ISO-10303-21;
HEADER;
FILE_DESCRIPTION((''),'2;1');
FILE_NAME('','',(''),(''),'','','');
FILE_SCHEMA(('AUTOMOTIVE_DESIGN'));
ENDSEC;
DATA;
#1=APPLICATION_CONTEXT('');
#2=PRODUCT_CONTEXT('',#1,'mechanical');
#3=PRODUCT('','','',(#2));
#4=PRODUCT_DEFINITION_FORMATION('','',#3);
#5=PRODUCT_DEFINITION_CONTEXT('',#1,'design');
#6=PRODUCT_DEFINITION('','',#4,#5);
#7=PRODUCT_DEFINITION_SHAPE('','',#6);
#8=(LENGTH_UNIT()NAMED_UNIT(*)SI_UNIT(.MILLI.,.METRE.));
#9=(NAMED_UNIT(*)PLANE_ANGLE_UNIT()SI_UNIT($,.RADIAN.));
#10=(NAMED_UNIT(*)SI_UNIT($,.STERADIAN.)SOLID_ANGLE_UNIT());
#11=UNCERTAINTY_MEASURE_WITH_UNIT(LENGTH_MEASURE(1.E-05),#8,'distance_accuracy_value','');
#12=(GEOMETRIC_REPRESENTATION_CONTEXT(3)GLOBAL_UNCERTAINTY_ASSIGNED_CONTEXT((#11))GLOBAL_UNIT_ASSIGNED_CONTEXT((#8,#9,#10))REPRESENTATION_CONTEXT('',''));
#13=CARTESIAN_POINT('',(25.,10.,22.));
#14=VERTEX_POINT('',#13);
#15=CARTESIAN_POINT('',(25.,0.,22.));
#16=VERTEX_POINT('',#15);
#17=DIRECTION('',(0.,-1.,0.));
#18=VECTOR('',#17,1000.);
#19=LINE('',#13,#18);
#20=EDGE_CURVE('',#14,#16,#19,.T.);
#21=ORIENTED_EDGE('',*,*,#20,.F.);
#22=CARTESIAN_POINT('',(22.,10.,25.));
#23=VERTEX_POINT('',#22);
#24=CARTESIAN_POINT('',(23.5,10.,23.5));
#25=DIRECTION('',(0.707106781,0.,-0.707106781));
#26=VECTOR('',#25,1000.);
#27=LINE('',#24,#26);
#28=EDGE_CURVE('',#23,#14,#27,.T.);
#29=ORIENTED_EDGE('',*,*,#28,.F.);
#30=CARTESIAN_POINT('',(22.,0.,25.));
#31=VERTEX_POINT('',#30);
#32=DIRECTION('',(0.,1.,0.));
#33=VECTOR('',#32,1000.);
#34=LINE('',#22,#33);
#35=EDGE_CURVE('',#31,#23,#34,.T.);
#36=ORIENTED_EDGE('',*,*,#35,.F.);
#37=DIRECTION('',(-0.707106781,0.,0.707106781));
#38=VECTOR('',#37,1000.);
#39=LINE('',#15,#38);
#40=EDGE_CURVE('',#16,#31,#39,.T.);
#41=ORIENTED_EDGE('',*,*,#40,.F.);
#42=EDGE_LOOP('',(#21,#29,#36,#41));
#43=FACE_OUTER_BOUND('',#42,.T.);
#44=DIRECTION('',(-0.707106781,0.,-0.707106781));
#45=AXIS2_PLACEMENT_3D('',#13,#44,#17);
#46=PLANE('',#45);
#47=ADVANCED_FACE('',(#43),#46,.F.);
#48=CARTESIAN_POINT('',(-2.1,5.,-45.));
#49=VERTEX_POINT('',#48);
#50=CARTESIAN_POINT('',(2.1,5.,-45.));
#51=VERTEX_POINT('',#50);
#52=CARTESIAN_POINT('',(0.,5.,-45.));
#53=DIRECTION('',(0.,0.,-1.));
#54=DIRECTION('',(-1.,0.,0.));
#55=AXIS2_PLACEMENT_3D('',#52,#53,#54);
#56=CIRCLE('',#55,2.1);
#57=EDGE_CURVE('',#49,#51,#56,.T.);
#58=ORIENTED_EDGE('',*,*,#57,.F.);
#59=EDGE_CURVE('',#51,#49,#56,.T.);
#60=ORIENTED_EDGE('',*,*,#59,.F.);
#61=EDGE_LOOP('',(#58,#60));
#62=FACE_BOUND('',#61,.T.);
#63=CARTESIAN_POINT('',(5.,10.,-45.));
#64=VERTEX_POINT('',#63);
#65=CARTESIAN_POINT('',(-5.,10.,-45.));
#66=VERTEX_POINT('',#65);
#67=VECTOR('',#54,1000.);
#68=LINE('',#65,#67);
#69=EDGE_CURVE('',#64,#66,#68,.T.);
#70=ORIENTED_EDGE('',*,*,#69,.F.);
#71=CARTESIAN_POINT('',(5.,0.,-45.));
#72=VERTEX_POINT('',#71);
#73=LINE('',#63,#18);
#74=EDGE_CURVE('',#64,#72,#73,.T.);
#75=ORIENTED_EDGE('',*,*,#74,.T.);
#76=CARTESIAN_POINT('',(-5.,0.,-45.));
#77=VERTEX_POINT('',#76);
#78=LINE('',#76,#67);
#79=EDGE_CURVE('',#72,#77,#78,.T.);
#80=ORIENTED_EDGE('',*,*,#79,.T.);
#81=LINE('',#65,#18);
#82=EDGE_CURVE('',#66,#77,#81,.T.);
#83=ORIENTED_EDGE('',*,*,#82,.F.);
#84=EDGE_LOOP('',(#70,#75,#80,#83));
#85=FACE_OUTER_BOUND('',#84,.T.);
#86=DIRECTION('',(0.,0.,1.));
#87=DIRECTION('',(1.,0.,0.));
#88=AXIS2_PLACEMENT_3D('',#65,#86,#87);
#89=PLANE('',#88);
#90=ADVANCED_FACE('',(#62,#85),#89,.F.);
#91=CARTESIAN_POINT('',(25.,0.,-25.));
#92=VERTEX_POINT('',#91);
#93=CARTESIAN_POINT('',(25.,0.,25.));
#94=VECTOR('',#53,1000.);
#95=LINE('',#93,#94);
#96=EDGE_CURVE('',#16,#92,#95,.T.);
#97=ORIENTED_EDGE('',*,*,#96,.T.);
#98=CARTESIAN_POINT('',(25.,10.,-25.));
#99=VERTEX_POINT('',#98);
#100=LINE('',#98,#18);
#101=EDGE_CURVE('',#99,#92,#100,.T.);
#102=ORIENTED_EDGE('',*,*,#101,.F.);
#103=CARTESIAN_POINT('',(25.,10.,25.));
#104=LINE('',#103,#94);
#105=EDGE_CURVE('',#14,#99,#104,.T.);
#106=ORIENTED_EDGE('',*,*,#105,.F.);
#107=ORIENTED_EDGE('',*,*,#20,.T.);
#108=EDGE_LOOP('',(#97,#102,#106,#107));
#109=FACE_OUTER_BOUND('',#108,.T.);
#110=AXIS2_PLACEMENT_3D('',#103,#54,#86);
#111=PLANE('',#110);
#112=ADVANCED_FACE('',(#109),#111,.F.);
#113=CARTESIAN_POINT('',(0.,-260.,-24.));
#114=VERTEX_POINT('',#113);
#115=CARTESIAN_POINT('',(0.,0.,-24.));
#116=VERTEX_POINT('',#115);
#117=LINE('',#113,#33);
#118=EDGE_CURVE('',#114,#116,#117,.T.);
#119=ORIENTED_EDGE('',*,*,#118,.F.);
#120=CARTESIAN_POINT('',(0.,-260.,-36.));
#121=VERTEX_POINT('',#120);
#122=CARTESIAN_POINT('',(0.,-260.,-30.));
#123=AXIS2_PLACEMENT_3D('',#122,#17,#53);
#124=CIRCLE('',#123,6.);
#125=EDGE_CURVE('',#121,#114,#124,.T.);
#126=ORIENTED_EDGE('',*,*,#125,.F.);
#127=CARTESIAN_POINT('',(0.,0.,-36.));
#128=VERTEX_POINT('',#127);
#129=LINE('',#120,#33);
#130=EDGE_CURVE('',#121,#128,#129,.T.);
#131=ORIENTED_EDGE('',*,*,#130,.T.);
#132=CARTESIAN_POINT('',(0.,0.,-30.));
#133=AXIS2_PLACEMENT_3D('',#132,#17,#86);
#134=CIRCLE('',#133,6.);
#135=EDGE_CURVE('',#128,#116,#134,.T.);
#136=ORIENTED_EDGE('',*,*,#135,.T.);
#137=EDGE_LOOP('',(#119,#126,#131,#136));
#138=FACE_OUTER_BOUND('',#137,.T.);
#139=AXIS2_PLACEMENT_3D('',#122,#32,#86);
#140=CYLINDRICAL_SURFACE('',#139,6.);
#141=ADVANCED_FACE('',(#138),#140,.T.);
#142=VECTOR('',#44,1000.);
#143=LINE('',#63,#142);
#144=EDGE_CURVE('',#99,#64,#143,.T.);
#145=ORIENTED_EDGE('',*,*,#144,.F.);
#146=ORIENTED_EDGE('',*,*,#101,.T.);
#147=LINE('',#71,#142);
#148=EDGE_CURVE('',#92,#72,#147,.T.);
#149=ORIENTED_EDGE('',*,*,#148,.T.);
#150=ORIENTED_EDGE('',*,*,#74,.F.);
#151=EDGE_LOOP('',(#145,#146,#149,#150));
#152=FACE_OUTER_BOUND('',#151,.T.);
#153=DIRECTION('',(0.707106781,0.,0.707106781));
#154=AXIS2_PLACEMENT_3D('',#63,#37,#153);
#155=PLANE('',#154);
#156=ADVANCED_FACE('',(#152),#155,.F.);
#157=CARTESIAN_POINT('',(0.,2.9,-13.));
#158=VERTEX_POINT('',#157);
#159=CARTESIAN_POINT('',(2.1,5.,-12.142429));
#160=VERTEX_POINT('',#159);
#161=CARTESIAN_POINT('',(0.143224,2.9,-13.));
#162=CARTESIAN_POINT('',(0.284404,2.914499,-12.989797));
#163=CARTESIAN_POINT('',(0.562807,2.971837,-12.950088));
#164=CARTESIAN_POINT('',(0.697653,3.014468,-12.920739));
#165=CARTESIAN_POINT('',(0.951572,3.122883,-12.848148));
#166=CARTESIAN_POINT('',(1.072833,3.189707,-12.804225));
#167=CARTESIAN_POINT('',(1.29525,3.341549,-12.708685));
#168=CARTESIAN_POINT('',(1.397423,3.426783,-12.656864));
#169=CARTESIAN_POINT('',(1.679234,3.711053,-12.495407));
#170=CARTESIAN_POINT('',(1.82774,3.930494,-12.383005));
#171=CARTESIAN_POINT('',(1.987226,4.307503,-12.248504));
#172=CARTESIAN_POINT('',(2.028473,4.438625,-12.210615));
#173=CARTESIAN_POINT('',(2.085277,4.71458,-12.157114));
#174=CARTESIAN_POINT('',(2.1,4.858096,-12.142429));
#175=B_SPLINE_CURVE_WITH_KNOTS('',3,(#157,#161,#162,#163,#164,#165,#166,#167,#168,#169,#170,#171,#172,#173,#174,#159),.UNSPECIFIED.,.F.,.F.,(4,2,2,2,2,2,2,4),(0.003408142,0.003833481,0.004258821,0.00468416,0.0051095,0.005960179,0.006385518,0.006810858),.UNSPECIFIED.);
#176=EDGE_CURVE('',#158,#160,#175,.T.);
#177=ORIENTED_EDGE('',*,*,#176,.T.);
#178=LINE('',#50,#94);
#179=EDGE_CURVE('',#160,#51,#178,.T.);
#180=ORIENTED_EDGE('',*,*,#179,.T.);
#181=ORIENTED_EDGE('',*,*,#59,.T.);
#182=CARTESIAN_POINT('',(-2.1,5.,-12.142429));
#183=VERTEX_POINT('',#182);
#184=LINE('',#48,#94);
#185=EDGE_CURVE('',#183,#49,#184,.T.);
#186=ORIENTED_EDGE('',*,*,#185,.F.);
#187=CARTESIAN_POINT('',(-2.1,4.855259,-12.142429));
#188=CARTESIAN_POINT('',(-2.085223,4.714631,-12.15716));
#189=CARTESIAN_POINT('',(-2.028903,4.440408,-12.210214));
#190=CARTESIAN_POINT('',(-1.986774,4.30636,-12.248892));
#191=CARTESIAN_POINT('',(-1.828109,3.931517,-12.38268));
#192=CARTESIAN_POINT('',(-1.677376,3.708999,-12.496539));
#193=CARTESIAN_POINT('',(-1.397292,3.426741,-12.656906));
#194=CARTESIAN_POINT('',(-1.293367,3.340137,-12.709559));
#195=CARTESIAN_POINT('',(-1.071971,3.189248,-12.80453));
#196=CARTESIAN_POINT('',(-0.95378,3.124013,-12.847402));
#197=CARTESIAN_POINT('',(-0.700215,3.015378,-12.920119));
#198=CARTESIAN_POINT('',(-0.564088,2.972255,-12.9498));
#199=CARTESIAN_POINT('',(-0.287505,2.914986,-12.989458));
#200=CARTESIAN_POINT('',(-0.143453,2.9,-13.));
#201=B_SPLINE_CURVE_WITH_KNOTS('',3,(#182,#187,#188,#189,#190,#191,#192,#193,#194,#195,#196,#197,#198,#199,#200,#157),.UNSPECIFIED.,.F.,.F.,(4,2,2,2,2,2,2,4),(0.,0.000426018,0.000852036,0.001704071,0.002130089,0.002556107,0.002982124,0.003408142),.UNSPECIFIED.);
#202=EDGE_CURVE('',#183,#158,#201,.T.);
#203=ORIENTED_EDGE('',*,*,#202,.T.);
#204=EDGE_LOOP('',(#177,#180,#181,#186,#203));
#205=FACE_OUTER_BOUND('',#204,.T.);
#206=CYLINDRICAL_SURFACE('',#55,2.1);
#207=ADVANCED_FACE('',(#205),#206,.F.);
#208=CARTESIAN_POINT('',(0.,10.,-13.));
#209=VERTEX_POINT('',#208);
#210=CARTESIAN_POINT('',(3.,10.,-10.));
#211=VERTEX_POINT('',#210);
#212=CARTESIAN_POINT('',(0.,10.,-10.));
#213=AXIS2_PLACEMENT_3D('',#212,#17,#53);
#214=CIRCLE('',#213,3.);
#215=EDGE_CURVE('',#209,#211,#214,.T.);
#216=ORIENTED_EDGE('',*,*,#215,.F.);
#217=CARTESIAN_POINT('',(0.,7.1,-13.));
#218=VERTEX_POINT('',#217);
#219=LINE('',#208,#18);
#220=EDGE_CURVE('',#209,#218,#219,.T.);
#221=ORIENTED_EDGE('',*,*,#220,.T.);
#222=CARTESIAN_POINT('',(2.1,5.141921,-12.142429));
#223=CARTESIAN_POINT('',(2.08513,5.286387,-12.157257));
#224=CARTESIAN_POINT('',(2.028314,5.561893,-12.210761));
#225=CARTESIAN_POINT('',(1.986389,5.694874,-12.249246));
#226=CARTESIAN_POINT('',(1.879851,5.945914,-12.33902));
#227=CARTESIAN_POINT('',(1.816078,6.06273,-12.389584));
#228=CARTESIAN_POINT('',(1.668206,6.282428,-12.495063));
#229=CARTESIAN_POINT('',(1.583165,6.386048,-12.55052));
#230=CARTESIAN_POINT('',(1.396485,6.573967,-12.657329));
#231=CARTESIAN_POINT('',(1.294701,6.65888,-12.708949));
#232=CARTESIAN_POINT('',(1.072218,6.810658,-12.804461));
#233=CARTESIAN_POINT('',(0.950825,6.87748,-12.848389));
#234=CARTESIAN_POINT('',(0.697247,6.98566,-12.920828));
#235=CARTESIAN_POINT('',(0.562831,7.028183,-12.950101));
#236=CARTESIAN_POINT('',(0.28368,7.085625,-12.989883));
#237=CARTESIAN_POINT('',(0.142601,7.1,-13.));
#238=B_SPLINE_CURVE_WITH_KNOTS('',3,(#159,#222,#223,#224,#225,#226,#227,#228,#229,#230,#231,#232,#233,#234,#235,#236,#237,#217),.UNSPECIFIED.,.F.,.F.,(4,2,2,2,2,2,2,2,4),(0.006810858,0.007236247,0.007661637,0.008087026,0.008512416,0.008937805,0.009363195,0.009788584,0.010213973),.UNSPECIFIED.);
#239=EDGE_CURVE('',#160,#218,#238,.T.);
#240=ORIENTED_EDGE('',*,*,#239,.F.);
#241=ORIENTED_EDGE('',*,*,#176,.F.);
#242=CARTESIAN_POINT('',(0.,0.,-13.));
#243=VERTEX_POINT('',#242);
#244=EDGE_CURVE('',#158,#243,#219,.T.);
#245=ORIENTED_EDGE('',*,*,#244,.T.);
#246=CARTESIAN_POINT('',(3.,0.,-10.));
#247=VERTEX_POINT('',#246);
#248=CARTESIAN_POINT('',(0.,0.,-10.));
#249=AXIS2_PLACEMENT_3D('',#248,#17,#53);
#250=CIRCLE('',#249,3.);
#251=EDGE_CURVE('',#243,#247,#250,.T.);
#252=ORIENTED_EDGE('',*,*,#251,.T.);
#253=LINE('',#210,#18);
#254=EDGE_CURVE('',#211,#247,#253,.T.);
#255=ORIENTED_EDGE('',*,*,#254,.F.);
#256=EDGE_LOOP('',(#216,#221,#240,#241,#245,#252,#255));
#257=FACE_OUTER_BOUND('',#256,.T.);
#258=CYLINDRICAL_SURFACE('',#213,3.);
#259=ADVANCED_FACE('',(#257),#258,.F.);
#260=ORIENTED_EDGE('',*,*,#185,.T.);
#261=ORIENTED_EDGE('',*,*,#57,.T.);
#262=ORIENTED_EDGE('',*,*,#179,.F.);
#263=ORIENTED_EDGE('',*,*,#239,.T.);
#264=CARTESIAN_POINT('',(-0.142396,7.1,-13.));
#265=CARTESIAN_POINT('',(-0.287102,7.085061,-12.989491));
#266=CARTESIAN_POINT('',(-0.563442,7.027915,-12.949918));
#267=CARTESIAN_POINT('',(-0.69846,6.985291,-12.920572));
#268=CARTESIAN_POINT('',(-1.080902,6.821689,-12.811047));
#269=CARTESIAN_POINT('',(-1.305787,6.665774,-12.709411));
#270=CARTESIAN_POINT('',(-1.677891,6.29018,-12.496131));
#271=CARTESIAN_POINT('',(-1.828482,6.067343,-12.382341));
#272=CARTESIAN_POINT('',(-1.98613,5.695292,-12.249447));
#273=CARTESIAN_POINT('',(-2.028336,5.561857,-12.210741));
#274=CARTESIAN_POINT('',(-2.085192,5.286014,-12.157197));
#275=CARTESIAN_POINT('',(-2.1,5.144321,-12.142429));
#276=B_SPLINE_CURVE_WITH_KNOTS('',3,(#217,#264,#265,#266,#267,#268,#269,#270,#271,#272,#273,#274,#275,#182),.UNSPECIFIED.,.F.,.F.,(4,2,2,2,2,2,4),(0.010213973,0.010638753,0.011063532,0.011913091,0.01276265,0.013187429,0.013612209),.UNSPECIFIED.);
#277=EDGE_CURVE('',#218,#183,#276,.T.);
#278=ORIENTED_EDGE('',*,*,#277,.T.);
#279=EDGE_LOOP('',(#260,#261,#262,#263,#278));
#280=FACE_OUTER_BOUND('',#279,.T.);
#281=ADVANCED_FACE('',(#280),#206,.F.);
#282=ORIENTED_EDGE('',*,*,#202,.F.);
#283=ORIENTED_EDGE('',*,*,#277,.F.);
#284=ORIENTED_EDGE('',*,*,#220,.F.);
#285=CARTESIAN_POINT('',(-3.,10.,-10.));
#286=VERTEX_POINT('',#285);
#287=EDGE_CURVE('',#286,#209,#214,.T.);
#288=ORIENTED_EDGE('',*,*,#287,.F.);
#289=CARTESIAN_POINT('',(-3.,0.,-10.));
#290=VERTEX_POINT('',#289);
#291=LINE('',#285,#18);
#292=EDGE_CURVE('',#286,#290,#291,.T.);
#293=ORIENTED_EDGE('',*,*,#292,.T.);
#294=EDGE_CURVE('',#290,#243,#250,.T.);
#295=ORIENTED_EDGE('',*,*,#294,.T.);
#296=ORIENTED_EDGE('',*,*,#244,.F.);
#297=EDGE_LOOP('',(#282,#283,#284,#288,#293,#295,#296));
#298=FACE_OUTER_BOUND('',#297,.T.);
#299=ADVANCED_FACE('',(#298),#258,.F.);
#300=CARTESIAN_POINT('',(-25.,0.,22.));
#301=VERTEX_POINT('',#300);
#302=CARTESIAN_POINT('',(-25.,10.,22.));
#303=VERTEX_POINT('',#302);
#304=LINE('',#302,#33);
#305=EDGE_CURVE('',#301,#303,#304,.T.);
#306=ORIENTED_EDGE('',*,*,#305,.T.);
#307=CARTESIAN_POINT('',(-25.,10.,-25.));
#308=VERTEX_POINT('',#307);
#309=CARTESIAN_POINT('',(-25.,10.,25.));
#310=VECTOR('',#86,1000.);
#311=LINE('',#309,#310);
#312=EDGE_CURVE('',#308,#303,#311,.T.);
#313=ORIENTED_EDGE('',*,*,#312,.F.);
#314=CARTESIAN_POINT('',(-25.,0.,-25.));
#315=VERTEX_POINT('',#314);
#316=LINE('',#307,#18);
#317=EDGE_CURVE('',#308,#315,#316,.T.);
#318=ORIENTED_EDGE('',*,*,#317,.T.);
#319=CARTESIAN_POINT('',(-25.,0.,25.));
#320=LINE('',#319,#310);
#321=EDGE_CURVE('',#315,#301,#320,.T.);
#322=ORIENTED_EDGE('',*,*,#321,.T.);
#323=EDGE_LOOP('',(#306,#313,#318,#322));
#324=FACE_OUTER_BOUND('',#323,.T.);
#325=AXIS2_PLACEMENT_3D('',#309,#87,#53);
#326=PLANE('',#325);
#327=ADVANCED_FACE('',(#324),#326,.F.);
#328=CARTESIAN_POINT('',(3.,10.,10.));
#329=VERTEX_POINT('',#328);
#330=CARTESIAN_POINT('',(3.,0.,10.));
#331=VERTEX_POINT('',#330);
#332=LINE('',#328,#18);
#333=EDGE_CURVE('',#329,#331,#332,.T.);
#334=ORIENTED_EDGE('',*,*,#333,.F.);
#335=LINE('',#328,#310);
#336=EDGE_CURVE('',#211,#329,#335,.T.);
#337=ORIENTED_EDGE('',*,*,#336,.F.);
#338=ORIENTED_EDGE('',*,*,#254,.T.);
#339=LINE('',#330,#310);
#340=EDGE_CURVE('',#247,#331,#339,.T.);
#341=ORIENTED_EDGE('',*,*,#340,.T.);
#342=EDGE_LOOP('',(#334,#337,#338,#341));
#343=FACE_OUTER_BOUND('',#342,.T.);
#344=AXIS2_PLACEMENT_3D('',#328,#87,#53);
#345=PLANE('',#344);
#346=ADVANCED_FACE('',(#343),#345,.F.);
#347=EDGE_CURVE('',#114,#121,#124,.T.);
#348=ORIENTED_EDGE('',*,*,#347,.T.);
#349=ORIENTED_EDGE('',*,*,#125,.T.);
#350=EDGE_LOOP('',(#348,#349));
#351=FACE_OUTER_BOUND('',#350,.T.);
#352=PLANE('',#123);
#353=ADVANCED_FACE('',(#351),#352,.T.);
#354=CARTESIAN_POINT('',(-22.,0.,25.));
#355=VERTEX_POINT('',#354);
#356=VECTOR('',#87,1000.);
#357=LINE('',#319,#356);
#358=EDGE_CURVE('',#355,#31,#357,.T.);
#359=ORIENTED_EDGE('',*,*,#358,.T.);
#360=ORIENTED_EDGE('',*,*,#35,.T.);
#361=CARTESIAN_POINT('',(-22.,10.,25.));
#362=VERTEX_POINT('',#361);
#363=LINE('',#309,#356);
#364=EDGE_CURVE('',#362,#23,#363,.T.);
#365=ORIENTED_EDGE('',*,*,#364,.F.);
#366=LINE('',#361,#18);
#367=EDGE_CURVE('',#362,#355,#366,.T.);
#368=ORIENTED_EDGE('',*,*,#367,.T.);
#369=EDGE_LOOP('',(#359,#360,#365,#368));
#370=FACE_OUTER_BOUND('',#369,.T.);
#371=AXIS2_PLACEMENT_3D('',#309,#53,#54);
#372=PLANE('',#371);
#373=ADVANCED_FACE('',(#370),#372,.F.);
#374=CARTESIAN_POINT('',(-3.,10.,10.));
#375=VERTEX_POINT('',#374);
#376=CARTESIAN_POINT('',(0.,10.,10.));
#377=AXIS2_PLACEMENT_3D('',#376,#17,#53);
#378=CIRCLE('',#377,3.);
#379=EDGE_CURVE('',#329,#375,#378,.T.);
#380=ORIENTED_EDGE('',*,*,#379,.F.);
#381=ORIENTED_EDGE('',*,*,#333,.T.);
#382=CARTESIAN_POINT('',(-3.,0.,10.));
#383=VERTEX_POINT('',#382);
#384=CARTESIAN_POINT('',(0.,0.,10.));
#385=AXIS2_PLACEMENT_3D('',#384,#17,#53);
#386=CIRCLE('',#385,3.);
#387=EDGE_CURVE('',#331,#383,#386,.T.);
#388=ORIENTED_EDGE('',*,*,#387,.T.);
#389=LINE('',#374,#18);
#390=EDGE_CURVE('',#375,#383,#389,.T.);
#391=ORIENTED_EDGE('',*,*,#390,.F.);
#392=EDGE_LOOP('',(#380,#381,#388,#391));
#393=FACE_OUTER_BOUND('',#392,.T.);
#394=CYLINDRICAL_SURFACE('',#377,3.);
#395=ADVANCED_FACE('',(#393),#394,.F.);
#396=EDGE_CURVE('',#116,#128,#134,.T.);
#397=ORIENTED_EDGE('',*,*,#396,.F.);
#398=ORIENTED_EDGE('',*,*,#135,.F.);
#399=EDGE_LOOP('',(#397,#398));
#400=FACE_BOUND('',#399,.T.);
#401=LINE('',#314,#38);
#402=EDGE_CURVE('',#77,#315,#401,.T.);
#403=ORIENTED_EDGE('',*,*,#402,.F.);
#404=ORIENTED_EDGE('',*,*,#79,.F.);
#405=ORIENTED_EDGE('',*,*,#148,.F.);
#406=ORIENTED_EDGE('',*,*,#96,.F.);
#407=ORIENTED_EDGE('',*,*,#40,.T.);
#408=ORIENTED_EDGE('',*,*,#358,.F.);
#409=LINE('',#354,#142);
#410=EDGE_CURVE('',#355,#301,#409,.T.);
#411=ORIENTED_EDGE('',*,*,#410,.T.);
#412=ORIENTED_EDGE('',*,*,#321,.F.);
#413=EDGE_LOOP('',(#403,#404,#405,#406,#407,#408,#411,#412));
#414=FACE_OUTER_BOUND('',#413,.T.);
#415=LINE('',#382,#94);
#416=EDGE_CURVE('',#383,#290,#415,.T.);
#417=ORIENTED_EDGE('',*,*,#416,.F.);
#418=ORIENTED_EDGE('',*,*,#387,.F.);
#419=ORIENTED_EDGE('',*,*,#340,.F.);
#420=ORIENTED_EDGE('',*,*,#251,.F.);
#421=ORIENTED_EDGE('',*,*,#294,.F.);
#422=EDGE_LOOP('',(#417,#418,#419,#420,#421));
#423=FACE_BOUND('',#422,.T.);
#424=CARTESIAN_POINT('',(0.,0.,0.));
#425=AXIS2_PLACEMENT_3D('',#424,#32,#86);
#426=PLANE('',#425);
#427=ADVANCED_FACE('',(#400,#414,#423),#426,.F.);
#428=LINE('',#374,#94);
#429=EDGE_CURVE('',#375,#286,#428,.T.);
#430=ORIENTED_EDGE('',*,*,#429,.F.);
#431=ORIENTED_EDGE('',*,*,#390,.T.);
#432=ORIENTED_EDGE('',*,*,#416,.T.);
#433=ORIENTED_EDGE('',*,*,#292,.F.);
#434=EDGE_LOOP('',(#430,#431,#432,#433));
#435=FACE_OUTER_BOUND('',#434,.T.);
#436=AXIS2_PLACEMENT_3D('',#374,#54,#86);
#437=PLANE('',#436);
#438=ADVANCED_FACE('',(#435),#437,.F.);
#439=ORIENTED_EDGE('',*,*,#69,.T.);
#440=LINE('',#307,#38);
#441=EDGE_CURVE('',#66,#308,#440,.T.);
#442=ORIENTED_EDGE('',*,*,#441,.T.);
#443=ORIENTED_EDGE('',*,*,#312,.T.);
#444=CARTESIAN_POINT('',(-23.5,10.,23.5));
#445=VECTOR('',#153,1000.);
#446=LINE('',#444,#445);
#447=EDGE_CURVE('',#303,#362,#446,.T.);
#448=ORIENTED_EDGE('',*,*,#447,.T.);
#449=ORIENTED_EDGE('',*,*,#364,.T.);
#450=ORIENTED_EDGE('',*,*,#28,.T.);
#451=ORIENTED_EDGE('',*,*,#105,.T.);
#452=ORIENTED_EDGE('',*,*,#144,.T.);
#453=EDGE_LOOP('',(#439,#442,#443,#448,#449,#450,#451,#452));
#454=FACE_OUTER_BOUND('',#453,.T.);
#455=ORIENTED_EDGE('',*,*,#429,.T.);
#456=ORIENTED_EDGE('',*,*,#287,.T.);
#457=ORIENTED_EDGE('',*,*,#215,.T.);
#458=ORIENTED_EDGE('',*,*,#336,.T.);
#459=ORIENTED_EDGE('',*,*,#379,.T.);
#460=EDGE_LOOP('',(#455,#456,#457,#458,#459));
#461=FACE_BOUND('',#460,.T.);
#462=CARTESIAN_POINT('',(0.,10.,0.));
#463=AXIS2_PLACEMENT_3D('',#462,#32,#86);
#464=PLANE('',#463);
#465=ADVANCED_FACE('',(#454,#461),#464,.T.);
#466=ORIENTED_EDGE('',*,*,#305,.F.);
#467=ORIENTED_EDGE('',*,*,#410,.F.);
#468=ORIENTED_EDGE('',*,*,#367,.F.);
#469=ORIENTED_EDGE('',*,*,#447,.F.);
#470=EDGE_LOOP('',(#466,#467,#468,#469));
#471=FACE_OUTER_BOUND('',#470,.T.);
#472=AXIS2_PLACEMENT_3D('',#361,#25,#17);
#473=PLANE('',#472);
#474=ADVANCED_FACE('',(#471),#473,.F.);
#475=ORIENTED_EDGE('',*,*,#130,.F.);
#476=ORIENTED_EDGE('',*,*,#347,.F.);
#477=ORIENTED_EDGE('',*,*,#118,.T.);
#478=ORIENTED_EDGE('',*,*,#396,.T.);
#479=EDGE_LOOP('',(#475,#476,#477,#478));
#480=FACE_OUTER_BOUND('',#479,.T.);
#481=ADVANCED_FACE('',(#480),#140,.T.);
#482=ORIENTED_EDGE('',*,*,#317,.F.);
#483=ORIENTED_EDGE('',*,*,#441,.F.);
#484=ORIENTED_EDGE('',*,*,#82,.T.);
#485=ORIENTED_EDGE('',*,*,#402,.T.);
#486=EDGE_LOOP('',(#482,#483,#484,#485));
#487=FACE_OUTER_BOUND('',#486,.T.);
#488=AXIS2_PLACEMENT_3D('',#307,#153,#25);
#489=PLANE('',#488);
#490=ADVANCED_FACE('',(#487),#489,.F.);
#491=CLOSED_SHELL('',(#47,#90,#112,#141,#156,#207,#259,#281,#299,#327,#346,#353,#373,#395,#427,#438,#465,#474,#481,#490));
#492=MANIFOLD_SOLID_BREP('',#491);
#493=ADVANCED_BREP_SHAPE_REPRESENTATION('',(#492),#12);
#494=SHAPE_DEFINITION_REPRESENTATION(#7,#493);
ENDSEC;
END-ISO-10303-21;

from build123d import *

# Parameters (mm, degrees)
BOSS_EXTRUDE1_DEPTH   = 10
SKETCH2_R             = 6
BOSS_EXTRUDE2_DEPTH   = 260
M5_TAPPED_HOLE1_D     = 4.2
M5_TAPPED_HOLE1_DEPTH = 36.9
M5_TAPPED_HOLE1_TIP   = 1.2618073
CUT_EXTRUDE1_DEPTH    = 266.047165614
CHAMFER1_SIZE         = 3


with BuildPart() as part:
    # Sketch1 → Boss-Extrude1 (new body)
    with BuildSketch(Plane(origin=(0, 0, 0), x_dir=(1, 0, 0), z_dir=(0, 1, 0))):
        Polygon((-25, 25), (-5, 45), (5, 45), (25, 25), (25, -25), (-25, -25), align=None)
    extrude(amount=BOSS_EXTRUDE1_DEPTH)

    # Sketch2 → Boss-Extrude2 (add)
    with BuildSketch(Plane.XZ):
        with Locations(Location((0, -30, 0), (0, 0, 90))):
            Circle(SKETCH2_R)
    extrude(amount=BOSS_EXTRUDE2_DEPTH)

    # M5 Tapped Hole1
    with Locations(Plane(origin=(0, 0, -45), x_dir=(-1, 0, 0), z_dir=(0, 0, -1))):
        with Locations((0, 5)):
            Hole(M5_TAPPED_HOLE1_D / 2, depth=M5_TAPPED_HOLE1_DEPTH)
            with Locations((0, 0, -(M5_TAPPED_HOLE1_DEPTH + M5_TAPPED_HOLE1_TIP / 2))):  # 118° drill point
                Cone(0, M5_TAPPED_HOLE1_D / 2, M5_TAPPED_HOLE1_TIP, mode=Mode.SUBTRACT)

    # Sketch5 → Cut-Extrude1 (cut, through all)
    with BuildSketch(Plane.XZ):
        with BuildLine():
            Line((3, 10), (3, -10))
            ThreePointArc((3, -10), (0, -13), (-3, -10))
            Line((-3, -10), (-3, 10))
            ThreePointArc((-3, 10), (0, 13), (3, 10))
        make_face()
    extrude(amount=-CUT_EXTRUDE1_DEPTH, mode=Mode.SUBTRACT)

    # Chamfer1
    chamfer1_edges = [part.edges().sort_by_distance(p)[0] for p in [
        (25, 5, 25),
        (-25, 5, 25),
    ]]
    chamfer(chamfer1_edges, length=CHAMFER1_SIZE)


solid = part.part
